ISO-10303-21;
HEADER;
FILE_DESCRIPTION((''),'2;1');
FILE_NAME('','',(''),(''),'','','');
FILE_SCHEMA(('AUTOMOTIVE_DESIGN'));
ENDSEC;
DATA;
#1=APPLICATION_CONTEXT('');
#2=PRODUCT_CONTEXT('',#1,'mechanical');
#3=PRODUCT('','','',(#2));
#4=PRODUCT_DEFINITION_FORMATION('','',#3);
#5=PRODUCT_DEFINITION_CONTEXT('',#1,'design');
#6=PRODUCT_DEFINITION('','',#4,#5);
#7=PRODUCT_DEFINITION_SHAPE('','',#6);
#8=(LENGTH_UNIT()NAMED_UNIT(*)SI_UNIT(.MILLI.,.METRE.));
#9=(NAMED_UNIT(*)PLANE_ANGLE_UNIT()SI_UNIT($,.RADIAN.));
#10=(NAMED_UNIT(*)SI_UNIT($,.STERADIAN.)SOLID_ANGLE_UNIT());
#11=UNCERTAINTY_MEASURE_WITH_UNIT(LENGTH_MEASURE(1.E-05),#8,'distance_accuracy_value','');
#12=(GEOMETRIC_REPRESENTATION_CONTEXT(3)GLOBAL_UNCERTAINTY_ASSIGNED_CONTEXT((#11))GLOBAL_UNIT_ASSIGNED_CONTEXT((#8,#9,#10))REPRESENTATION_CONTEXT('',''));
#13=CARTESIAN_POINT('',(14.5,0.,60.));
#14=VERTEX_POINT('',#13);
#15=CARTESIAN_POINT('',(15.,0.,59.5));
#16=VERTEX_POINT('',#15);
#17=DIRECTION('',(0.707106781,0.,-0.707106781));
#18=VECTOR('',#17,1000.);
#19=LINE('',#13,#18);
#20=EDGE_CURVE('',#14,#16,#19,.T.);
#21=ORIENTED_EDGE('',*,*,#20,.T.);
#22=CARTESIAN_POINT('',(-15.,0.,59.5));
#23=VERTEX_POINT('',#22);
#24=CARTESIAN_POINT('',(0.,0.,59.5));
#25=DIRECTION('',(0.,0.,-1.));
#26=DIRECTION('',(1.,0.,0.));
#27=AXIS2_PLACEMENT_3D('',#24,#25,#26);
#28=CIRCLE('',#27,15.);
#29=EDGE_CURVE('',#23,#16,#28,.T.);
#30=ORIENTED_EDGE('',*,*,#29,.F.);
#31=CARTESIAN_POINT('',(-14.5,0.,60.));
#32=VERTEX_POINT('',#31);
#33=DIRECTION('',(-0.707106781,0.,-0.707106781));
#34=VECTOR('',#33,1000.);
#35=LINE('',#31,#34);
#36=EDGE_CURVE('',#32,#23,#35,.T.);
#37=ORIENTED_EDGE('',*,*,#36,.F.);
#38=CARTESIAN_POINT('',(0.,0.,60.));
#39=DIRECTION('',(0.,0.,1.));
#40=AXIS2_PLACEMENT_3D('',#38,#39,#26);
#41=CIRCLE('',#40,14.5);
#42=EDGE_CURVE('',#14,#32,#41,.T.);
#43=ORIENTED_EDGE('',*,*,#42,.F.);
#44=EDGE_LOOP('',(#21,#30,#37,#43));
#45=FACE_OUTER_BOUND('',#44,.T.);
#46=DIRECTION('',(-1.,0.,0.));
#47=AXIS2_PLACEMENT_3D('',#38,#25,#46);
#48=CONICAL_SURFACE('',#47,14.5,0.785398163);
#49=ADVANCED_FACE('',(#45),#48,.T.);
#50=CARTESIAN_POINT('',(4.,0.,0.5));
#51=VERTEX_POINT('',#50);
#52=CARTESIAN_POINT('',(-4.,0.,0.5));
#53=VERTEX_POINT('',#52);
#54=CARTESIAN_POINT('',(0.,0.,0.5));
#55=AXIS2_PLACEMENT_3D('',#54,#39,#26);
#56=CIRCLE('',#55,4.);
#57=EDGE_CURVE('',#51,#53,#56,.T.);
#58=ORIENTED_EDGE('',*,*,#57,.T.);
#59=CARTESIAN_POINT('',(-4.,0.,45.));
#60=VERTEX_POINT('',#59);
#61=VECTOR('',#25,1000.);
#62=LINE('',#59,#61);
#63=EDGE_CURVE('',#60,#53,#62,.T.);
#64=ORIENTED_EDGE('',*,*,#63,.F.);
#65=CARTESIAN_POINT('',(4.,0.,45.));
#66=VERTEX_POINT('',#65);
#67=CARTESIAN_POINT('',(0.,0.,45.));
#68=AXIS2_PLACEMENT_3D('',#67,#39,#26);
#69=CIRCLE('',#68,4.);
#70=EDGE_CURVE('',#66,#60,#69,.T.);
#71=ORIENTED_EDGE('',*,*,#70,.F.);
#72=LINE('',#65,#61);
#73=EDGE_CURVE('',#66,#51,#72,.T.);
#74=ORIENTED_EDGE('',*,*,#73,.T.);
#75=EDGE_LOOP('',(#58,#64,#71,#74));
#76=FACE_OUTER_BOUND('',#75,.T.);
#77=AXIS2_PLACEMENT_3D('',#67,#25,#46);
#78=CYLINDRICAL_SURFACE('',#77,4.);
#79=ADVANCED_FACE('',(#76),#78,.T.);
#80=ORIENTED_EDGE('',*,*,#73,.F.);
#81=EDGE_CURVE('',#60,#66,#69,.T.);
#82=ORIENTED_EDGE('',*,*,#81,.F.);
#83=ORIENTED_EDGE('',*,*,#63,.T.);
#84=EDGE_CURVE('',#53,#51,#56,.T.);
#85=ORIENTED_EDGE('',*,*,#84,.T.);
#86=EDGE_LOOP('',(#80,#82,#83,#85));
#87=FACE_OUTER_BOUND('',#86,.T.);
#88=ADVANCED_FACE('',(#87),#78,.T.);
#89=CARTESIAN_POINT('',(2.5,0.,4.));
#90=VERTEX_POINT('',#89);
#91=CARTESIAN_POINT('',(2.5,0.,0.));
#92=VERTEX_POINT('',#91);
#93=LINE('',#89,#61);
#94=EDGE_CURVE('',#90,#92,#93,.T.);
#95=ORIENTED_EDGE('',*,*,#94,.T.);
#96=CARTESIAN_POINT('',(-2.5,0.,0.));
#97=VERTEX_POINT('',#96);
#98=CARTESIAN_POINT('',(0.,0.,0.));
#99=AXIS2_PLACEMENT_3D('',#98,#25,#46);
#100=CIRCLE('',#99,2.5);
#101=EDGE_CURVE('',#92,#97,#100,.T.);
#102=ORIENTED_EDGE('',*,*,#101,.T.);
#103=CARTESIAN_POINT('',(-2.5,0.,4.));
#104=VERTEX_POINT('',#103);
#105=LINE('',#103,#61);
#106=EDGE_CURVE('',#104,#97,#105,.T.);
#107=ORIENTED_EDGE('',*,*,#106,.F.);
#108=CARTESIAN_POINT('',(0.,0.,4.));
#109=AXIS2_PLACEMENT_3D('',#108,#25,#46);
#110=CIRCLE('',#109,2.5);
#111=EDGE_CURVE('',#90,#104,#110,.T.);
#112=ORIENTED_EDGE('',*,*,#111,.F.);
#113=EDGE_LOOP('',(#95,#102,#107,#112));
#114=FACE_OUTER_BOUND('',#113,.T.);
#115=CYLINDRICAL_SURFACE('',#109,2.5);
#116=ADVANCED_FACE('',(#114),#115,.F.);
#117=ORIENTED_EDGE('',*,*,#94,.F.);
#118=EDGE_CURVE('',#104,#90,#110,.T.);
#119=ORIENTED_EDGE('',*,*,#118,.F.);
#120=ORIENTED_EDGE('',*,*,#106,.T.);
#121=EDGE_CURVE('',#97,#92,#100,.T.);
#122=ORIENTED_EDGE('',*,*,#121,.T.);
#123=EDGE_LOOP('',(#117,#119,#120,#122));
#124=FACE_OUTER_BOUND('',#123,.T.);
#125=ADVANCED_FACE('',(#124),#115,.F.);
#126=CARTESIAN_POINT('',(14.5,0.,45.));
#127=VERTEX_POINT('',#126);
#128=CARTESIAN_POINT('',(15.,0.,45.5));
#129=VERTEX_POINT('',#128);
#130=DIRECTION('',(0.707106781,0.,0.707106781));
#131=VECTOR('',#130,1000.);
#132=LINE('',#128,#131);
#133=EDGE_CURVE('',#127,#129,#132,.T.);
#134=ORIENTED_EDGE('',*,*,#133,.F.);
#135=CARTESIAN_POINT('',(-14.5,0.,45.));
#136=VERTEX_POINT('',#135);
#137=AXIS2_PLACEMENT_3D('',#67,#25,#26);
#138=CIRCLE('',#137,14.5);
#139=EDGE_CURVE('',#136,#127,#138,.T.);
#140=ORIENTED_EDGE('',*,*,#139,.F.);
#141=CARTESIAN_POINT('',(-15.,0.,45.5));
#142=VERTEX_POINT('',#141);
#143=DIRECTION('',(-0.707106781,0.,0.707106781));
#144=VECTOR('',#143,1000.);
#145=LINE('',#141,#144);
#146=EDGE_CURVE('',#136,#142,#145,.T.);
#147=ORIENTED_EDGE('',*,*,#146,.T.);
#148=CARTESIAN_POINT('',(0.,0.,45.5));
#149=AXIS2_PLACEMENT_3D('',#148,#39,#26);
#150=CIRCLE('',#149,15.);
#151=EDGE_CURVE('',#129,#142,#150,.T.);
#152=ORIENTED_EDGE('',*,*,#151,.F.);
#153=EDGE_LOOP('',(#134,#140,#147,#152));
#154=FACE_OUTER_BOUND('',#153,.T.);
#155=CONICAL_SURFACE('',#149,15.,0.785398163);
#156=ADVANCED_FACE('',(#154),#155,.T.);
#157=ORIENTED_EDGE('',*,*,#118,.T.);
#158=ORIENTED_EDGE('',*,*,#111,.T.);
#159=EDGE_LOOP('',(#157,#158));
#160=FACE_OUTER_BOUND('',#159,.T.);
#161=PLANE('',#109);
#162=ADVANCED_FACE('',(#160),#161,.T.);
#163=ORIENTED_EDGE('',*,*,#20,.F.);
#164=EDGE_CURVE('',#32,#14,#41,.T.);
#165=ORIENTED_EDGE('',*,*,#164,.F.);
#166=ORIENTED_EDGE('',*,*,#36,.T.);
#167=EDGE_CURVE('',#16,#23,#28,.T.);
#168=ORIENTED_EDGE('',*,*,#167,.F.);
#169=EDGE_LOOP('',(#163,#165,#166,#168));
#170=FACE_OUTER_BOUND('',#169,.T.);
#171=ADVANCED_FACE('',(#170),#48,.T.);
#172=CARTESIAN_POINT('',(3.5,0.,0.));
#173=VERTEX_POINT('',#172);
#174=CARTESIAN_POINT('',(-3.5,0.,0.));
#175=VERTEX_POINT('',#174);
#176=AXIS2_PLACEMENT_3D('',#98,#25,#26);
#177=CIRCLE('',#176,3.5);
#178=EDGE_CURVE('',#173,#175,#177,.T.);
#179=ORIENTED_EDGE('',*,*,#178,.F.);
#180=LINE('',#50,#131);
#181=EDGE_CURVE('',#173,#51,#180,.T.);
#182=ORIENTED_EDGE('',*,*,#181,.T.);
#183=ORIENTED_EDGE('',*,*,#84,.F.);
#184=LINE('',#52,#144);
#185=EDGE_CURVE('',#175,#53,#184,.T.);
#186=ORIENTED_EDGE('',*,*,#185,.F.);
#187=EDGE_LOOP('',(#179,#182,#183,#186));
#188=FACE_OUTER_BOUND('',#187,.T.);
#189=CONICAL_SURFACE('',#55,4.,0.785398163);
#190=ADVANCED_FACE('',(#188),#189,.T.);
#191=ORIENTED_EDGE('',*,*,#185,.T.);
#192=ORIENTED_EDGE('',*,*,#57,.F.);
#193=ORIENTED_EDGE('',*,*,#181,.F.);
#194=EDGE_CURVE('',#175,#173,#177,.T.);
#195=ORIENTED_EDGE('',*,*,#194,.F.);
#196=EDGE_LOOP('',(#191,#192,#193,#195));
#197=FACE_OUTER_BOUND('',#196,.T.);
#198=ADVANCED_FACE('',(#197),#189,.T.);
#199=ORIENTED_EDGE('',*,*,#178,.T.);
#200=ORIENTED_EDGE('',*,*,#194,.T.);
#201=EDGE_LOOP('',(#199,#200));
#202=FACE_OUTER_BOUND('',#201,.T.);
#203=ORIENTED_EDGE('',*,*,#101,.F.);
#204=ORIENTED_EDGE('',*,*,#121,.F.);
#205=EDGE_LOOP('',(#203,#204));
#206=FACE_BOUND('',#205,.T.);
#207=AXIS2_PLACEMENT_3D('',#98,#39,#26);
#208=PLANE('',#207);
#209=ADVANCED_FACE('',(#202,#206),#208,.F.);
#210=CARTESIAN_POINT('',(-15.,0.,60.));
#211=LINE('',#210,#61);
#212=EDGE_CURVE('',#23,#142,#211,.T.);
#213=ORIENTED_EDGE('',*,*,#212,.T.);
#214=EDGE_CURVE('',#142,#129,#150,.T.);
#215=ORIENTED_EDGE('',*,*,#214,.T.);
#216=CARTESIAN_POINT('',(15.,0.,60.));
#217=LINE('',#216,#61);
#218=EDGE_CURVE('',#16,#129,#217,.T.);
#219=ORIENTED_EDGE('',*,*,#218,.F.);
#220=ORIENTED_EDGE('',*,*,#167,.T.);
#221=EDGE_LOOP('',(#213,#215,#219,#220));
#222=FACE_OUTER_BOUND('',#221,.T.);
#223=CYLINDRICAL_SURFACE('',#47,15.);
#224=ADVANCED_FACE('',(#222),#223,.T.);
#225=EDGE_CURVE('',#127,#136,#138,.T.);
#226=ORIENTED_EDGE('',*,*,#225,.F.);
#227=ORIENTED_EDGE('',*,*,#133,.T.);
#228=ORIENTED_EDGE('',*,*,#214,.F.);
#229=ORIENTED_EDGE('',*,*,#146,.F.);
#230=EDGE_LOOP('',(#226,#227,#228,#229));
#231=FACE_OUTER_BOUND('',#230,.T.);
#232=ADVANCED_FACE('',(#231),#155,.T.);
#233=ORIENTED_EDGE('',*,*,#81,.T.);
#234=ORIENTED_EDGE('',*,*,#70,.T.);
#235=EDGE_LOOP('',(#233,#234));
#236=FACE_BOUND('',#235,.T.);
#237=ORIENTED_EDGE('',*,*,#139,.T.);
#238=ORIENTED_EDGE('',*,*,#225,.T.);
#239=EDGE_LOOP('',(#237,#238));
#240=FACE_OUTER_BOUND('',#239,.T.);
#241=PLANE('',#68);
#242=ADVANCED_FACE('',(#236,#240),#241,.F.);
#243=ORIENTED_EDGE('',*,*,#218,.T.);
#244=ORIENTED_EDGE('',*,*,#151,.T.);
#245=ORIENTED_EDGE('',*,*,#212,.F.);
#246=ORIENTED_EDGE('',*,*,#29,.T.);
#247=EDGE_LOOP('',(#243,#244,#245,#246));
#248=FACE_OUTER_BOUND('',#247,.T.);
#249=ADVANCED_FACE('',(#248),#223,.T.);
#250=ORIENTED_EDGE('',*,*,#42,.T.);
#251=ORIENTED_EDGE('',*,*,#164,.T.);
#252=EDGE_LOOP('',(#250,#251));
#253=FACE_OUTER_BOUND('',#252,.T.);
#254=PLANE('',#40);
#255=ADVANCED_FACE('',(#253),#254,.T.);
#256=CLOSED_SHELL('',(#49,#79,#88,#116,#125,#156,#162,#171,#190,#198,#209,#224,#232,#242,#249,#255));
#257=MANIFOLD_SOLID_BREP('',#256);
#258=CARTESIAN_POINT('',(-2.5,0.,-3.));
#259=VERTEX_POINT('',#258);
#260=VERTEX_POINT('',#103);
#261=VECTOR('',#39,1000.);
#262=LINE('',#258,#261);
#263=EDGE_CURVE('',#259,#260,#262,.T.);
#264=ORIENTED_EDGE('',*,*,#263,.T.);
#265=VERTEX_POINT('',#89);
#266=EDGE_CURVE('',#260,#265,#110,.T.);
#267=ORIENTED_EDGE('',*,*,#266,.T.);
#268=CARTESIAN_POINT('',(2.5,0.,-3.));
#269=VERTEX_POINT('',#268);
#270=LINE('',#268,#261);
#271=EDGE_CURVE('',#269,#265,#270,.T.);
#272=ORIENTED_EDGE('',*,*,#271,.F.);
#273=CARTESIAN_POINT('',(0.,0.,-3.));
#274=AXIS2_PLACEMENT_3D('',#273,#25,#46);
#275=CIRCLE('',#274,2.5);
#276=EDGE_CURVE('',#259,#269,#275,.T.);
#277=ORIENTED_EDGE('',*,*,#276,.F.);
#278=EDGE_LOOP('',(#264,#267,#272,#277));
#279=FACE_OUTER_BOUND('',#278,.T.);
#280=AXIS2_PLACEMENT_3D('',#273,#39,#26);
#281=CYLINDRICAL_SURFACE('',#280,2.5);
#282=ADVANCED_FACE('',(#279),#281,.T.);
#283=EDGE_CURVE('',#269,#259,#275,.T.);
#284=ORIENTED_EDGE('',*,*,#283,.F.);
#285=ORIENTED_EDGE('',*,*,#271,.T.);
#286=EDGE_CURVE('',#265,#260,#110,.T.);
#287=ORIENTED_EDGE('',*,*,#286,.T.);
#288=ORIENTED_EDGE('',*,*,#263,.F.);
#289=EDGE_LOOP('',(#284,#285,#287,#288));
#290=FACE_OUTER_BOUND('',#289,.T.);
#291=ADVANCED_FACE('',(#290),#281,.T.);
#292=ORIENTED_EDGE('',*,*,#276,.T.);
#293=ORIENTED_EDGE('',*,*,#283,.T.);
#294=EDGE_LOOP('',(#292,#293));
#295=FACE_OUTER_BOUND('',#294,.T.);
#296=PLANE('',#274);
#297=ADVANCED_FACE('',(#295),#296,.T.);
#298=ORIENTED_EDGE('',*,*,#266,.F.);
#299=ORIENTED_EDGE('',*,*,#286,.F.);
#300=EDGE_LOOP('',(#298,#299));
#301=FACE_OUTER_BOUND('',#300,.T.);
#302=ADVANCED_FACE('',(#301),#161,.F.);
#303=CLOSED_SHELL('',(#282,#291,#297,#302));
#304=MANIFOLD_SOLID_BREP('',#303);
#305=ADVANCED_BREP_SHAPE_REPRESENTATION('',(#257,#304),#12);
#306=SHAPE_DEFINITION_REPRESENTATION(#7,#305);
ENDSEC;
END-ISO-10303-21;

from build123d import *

# Parameters (mm, degrees)
SKETCH1_R           = 4
BOSS_EXTRUDE1_DEPTH = 45
SKETCH2_R           = 15
BOSS_EXTRUDE2_DEPTH = 15
SKETCH3_R           = 2.5
CUT_EXTRUDE1_DEPTH  = 4
SKETCH4_R           = 2.5
BOSS_EXTRUDE3_DEPTH = 7
CHAMFER1_SIZE       = 0.5


with BuildPart() as part:
    # Sketch1 → Boss-Extrude1 (new body)
    with BuildSketch(Plane.XY):
        with Locations(Location((0, 0, 0), (0, 0, 180))):
            Circle(SKETCH1_R)
    extrude(amount=BOSS_EXTRUDE1_DEPTH)

    # Sketch2 → Boss-Extrude2 (add)
    with BuildSketch(Plane.XY.offset(45)):
        Circle(SKETCH2_R)
    extrude(amount=BOSS_EXTRUDE2_DEPTH)

    # Sketch3 → Cut-Extrude1 (cut)
    with BuildSketch(Plane(origin=(0, 0, 0), x_dir=(-1, 0, 0), z_dir=(0, 0, -1))):
        Circle(SKETCH3_R)
    extrude(amount=-CUT_EXTRUDE1_DEPTH, mode=Mode.SUBTRACT)

    # Chamfer1
    chamfer1_edges = [part.edges().sort_by_distance(p)[0] for p in [
        (4, 0, 0),
        (-15, 0, 45),
        (-15, 0, 60),
    ]]
    chamfer(chamfer1_edges, length=CHAMFER1_SIZE)


with BuildPart() as body_2:
    # Sketch4 → Boss-Extrude3 (new body)
    with BuildSketch(Plane(origin=(0, 0, 4), x_dir=(-1, 0, 0), z_dir=(0, 0, -1))):
        Circle(SKETCH4_R)
    extrude(amount=BOSS_EXTRUDE3_DEPTH)


solid = Compound([part.part, body_2.part])
